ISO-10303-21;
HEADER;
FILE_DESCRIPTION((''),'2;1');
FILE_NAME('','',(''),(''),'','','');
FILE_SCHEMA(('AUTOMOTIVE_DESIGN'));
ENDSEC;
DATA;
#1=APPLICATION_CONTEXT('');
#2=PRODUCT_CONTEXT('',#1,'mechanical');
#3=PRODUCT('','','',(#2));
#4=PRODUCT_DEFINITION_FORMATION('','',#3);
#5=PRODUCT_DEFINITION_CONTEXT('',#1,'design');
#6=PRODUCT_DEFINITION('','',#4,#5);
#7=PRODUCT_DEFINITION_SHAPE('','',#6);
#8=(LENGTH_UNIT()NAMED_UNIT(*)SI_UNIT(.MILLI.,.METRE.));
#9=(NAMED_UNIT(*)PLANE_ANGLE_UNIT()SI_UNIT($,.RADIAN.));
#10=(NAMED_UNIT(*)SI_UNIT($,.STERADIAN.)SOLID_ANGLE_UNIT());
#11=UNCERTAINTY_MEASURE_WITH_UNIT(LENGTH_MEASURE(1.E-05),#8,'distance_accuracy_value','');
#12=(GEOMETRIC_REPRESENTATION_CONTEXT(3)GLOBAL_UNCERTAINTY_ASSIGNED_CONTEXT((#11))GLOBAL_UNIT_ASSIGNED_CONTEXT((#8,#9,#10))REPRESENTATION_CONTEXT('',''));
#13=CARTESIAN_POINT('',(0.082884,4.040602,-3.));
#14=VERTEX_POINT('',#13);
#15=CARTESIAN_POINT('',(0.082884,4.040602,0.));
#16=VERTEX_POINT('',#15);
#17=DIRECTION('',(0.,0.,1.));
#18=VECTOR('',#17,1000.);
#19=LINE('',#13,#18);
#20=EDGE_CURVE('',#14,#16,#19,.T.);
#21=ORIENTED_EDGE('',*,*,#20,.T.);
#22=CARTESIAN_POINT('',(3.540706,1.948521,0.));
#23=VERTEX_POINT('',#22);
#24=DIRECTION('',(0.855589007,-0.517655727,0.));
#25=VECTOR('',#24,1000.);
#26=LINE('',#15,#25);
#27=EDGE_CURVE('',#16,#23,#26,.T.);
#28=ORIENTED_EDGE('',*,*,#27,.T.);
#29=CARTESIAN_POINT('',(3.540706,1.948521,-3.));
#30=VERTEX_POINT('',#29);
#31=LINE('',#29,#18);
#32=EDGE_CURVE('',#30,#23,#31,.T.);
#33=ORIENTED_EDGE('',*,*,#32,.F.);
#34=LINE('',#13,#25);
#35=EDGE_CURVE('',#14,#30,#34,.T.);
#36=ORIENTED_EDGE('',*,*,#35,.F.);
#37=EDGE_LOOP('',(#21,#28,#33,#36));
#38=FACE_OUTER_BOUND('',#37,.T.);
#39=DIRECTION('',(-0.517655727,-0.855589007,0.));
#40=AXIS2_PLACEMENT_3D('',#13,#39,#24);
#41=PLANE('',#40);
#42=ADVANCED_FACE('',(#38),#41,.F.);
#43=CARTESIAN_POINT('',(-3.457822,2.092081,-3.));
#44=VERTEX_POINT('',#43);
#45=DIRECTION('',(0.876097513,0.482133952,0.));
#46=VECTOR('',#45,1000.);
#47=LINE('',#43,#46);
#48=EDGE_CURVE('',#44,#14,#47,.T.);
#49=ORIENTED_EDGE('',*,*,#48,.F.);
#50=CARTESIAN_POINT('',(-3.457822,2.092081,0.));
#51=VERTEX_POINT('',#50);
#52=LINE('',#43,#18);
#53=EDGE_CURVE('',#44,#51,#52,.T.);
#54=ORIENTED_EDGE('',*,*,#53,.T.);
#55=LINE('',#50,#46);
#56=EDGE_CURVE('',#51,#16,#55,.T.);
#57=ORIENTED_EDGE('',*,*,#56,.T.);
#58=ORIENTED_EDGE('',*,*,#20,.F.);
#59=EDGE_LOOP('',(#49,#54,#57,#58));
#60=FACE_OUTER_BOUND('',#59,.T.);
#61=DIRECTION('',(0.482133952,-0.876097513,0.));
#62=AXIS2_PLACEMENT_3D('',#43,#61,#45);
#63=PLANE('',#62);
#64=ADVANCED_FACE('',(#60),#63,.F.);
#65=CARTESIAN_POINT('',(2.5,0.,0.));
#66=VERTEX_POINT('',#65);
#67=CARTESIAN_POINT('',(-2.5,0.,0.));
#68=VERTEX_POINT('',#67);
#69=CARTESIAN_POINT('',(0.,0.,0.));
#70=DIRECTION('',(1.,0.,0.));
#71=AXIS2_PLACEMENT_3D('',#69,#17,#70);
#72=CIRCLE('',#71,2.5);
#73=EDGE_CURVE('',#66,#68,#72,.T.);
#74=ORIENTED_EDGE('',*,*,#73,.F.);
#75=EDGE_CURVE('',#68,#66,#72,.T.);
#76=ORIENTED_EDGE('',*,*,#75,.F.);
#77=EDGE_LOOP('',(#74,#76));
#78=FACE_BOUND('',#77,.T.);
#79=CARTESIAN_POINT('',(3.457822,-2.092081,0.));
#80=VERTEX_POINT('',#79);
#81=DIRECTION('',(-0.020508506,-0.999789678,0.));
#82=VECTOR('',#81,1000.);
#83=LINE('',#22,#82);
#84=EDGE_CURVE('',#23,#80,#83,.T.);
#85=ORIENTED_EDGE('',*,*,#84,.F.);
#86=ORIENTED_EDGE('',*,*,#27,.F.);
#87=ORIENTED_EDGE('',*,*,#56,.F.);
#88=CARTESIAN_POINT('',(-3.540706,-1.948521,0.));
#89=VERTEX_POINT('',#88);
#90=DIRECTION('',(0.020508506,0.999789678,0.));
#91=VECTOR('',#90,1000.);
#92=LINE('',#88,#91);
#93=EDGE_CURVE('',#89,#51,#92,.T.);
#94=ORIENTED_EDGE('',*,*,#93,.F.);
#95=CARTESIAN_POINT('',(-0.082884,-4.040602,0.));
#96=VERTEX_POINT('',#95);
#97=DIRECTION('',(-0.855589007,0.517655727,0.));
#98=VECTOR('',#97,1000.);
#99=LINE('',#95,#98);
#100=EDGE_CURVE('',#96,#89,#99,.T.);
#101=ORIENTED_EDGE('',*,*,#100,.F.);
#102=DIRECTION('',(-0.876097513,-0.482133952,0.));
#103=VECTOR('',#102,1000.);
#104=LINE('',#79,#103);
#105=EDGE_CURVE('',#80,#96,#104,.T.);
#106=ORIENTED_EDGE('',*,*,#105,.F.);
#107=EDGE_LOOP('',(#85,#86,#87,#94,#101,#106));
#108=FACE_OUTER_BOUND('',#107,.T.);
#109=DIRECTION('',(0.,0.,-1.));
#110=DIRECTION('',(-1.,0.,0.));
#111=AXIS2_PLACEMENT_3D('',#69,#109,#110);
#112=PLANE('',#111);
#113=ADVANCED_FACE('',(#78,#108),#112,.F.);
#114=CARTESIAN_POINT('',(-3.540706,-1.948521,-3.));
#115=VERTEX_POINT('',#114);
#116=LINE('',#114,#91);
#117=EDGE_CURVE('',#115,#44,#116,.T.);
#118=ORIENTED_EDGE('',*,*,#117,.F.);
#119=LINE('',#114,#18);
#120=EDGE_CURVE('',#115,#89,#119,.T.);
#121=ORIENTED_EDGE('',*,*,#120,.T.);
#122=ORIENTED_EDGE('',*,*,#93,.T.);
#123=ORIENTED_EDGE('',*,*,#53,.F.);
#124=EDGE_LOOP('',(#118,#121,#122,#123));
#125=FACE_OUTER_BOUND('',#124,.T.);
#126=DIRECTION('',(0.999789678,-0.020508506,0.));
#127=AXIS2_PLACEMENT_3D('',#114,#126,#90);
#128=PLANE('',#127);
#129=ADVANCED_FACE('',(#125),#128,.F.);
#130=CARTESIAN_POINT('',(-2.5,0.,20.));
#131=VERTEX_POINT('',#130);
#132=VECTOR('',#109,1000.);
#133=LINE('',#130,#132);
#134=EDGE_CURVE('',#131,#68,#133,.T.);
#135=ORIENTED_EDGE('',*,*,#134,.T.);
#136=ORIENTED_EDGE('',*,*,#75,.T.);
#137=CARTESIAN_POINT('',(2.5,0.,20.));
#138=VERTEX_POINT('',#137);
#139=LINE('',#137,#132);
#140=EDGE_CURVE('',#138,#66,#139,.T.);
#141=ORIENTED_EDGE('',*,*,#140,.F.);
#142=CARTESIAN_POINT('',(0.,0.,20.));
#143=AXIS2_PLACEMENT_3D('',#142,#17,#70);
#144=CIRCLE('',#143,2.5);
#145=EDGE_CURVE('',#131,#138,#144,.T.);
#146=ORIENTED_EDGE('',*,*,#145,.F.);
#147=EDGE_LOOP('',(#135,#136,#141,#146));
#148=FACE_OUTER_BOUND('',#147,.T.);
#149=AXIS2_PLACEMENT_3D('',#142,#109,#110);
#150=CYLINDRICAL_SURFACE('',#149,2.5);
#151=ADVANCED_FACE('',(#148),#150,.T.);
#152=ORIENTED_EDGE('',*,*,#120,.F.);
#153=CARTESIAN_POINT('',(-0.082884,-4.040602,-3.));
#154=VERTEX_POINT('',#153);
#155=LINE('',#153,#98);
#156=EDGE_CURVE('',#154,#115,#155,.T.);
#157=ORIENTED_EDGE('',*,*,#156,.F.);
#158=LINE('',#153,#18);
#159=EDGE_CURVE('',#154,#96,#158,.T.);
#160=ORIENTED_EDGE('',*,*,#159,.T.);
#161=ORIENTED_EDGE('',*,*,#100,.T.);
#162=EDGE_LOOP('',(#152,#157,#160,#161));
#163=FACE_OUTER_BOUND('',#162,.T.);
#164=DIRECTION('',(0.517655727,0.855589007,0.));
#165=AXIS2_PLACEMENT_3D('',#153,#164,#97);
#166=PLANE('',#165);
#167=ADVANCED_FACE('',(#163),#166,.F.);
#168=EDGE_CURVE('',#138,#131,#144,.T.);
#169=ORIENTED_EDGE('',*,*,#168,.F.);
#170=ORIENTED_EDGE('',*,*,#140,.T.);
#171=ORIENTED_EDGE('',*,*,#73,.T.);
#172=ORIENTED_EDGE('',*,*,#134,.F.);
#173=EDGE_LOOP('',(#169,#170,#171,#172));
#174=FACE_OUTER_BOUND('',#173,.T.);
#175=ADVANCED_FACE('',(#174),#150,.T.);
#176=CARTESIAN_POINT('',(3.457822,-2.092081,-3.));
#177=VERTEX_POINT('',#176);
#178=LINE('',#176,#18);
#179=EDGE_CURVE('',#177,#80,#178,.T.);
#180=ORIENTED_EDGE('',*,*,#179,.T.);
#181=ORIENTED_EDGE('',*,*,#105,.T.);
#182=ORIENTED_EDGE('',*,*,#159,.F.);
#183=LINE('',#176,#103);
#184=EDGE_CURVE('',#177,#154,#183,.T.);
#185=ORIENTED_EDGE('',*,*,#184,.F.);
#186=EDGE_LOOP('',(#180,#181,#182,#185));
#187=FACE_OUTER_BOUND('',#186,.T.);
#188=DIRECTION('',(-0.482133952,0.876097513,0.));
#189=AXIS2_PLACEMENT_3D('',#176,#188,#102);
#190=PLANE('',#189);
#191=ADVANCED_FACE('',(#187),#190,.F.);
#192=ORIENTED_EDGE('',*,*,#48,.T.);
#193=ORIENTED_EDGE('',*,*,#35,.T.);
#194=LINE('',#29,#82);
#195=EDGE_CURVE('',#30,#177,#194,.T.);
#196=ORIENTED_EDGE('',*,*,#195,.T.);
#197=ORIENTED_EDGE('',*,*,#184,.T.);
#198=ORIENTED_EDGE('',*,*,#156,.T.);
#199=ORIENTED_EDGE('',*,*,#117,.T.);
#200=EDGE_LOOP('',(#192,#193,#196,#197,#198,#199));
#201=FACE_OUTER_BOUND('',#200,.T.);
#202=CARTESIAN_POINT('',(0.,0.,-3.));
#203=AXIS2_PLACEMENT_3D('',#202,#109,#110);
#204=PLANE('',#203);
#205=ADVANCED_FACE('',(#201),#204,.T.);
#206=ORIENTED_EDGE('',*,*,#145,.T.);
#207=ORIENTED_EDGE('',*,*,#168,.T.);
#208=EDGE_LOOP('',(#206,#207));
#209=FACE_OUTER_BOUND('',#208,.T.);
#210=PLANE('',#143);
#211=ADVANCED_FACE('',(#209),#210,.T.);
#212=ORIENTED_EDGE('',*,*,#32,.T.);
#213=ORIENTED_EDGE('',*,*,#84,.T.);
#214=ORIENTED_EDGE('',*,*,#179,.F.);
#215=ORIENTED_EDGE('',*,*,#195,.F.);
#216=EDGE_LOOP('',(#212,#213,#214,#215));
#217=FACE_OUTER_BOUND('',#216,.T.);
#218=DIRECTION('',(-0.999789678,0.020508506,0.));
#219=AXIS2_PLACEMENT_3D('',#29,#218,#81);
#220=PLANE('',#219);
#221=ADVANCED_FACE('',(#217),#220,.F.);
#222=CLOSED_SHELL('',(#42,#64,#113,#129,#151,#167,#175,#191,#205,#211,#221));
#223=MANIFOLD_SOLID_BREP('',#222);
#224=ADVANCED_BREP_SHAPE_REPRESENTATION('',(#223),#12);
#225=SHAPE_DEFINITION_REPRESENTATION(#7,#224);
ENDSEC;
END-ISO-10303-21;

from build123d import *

# Parameters (mm, degrees)
SKETCH_1_R      = 2.5
EXTRUDE_1_DEPTH = 20
EXTRUDE_2_DEPTH = 3


with BuildPart() as part:
    # 草图1 → 凸台-拉伸1 (new body)
    with BuildSketch(Plane.XY):
        Circle(SKETCH_1_R)
    extrude(amount=EXTRUDE_1_DEPTH)

    # 草图2 → 凸台-拉伸2 (add)
    with BuildSketch(Plane(origin=(0, 0, 0), x_dir=(-1, 0, 0), z_dir=(0, 0, -1))):
        Polygon((0.082884141, -4.04060188), (3.540705945, -1.948521168), (3.457821804, 2.092080712), (-0.082884141, 4.04060188), (-3.540705945, 1.948521168), (-3.457821804, -2.092080712), align=None)
    extrude(amount=EXTRUDE_2_DEPTH)


solid = part.part
